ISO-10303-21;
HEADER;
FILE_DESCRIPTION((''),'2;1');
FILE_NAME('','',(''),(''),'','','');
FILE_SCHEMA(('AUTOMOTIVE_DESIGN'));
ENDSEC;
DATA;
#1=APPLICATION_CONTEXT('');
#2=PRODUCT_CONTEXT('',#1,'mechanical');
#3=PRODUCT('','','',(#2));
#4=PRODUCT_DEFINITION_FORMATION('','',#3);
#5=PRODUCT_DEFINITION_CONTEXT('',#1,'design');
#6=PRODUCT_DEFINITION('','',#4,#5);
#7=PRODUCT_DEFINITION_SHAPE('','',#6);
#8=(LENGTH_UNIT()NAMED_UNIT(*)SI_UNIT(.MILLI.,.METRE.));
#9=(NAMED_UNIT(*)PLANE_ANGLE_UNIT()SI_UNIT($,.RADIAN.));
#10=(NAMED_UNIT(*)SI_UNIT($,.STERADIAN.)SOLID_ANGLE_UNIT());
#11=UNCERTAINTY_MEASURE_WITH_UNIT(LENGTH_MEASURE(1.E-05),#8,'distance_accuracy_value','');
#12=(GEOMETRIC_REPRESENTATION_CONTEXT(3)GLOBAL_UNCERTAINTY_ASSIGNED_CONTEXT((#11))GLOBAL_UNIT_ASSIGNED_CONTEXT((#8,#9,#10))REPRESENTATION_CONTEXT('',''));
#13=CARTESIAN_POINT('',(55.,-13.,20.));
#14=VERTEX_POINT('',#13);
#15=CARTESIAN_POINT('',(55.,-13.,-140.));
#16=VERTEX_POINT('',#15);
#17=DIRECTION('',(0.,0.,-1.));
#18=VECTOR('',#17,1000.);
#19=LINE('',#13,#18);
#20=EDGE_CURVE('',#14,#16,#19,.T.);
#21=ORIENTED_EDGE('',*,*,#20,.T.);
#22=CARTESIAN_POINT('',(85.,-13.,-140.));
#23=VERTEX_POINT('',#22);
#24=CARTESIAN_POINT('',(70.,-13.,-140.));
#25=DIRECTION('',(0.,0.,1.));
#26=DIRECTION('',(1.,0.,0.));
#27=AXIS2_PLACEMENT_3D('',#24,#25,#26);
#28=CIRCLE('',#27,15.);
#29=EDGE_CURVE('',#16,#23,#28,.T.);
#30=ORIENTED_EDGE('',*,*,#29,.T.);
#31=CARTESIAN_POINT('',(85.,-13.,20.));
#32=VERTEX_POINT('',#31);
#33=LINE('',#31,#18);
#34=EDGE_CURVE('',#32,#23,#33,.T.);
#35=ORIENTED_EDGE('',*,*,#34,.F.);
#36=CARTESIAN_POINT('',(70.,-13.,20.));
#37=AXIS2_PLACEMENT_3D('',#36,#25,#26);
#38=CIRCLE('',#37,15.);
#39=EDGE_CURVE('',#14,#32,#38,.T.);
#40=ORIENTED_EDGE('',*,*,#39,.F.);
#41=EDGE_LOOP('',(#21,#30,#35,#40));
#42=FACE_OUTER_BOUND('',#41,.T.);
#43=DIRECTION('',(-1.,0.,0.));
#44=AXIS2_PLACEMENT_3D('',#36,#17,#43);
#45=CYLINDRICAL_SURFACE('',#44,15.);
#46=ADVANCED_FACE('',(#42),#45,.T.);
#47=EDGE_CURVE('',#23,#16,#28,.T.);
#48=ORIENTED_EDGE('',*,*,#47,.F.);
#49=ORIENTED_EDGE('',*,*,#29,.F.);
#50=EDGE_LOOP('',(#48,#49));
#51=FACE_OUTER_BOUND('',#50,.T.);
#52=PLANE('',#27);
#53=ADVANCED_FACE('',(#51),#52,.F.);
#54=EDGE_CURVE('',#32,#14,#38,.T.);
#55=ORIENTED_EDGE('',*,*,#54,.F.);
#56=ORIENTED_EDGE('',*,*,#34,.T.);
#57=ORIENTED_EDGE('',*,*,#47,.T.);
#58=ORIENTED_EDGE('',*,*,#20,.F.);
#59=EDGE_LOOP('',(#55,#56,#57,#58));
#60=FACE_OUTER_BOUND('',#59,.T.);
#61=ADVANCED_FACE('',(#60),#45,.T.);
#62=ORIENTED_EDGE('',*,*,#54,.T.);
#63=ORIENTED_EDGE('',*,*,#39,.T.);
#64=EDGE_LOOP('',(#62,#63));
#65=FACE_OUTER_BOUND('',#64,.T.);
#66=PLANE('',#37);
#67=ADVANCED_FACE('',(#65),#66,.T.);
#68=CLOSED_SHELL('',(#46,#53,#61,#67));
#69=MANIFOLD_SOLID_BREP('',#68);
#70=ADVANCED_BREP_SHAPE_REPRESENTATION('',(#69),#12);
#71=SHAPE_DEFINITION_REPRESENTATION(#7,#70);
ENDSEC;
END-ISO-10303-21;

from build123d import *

# Parameters (mm, degrees)
BOSS_EXTRUDE1_DEPTH      = 20
BOSS_EXTRUDE1_DEPTH_BACK = 140
SKETCH1_R                = 15


with BuildPart() as part:
    # Sketch1 → Boss-Extrude1 (new, two sides: drawn at the far end of the back side and taken through both)
    with BuildSketch(Plane.XY.offset(-BOSS_EXTRUDE1_DEPTH_BACK)):
        with Locations(Location((70, -13, 0), (0, 0, 180))):
            Circle(SKETCH1_R)
    extrude(amount=BOSS_EXTRUDE1_DEPTH + BOSS_EXTRUDE1_DEPTH_BACK)


solid = part.part
